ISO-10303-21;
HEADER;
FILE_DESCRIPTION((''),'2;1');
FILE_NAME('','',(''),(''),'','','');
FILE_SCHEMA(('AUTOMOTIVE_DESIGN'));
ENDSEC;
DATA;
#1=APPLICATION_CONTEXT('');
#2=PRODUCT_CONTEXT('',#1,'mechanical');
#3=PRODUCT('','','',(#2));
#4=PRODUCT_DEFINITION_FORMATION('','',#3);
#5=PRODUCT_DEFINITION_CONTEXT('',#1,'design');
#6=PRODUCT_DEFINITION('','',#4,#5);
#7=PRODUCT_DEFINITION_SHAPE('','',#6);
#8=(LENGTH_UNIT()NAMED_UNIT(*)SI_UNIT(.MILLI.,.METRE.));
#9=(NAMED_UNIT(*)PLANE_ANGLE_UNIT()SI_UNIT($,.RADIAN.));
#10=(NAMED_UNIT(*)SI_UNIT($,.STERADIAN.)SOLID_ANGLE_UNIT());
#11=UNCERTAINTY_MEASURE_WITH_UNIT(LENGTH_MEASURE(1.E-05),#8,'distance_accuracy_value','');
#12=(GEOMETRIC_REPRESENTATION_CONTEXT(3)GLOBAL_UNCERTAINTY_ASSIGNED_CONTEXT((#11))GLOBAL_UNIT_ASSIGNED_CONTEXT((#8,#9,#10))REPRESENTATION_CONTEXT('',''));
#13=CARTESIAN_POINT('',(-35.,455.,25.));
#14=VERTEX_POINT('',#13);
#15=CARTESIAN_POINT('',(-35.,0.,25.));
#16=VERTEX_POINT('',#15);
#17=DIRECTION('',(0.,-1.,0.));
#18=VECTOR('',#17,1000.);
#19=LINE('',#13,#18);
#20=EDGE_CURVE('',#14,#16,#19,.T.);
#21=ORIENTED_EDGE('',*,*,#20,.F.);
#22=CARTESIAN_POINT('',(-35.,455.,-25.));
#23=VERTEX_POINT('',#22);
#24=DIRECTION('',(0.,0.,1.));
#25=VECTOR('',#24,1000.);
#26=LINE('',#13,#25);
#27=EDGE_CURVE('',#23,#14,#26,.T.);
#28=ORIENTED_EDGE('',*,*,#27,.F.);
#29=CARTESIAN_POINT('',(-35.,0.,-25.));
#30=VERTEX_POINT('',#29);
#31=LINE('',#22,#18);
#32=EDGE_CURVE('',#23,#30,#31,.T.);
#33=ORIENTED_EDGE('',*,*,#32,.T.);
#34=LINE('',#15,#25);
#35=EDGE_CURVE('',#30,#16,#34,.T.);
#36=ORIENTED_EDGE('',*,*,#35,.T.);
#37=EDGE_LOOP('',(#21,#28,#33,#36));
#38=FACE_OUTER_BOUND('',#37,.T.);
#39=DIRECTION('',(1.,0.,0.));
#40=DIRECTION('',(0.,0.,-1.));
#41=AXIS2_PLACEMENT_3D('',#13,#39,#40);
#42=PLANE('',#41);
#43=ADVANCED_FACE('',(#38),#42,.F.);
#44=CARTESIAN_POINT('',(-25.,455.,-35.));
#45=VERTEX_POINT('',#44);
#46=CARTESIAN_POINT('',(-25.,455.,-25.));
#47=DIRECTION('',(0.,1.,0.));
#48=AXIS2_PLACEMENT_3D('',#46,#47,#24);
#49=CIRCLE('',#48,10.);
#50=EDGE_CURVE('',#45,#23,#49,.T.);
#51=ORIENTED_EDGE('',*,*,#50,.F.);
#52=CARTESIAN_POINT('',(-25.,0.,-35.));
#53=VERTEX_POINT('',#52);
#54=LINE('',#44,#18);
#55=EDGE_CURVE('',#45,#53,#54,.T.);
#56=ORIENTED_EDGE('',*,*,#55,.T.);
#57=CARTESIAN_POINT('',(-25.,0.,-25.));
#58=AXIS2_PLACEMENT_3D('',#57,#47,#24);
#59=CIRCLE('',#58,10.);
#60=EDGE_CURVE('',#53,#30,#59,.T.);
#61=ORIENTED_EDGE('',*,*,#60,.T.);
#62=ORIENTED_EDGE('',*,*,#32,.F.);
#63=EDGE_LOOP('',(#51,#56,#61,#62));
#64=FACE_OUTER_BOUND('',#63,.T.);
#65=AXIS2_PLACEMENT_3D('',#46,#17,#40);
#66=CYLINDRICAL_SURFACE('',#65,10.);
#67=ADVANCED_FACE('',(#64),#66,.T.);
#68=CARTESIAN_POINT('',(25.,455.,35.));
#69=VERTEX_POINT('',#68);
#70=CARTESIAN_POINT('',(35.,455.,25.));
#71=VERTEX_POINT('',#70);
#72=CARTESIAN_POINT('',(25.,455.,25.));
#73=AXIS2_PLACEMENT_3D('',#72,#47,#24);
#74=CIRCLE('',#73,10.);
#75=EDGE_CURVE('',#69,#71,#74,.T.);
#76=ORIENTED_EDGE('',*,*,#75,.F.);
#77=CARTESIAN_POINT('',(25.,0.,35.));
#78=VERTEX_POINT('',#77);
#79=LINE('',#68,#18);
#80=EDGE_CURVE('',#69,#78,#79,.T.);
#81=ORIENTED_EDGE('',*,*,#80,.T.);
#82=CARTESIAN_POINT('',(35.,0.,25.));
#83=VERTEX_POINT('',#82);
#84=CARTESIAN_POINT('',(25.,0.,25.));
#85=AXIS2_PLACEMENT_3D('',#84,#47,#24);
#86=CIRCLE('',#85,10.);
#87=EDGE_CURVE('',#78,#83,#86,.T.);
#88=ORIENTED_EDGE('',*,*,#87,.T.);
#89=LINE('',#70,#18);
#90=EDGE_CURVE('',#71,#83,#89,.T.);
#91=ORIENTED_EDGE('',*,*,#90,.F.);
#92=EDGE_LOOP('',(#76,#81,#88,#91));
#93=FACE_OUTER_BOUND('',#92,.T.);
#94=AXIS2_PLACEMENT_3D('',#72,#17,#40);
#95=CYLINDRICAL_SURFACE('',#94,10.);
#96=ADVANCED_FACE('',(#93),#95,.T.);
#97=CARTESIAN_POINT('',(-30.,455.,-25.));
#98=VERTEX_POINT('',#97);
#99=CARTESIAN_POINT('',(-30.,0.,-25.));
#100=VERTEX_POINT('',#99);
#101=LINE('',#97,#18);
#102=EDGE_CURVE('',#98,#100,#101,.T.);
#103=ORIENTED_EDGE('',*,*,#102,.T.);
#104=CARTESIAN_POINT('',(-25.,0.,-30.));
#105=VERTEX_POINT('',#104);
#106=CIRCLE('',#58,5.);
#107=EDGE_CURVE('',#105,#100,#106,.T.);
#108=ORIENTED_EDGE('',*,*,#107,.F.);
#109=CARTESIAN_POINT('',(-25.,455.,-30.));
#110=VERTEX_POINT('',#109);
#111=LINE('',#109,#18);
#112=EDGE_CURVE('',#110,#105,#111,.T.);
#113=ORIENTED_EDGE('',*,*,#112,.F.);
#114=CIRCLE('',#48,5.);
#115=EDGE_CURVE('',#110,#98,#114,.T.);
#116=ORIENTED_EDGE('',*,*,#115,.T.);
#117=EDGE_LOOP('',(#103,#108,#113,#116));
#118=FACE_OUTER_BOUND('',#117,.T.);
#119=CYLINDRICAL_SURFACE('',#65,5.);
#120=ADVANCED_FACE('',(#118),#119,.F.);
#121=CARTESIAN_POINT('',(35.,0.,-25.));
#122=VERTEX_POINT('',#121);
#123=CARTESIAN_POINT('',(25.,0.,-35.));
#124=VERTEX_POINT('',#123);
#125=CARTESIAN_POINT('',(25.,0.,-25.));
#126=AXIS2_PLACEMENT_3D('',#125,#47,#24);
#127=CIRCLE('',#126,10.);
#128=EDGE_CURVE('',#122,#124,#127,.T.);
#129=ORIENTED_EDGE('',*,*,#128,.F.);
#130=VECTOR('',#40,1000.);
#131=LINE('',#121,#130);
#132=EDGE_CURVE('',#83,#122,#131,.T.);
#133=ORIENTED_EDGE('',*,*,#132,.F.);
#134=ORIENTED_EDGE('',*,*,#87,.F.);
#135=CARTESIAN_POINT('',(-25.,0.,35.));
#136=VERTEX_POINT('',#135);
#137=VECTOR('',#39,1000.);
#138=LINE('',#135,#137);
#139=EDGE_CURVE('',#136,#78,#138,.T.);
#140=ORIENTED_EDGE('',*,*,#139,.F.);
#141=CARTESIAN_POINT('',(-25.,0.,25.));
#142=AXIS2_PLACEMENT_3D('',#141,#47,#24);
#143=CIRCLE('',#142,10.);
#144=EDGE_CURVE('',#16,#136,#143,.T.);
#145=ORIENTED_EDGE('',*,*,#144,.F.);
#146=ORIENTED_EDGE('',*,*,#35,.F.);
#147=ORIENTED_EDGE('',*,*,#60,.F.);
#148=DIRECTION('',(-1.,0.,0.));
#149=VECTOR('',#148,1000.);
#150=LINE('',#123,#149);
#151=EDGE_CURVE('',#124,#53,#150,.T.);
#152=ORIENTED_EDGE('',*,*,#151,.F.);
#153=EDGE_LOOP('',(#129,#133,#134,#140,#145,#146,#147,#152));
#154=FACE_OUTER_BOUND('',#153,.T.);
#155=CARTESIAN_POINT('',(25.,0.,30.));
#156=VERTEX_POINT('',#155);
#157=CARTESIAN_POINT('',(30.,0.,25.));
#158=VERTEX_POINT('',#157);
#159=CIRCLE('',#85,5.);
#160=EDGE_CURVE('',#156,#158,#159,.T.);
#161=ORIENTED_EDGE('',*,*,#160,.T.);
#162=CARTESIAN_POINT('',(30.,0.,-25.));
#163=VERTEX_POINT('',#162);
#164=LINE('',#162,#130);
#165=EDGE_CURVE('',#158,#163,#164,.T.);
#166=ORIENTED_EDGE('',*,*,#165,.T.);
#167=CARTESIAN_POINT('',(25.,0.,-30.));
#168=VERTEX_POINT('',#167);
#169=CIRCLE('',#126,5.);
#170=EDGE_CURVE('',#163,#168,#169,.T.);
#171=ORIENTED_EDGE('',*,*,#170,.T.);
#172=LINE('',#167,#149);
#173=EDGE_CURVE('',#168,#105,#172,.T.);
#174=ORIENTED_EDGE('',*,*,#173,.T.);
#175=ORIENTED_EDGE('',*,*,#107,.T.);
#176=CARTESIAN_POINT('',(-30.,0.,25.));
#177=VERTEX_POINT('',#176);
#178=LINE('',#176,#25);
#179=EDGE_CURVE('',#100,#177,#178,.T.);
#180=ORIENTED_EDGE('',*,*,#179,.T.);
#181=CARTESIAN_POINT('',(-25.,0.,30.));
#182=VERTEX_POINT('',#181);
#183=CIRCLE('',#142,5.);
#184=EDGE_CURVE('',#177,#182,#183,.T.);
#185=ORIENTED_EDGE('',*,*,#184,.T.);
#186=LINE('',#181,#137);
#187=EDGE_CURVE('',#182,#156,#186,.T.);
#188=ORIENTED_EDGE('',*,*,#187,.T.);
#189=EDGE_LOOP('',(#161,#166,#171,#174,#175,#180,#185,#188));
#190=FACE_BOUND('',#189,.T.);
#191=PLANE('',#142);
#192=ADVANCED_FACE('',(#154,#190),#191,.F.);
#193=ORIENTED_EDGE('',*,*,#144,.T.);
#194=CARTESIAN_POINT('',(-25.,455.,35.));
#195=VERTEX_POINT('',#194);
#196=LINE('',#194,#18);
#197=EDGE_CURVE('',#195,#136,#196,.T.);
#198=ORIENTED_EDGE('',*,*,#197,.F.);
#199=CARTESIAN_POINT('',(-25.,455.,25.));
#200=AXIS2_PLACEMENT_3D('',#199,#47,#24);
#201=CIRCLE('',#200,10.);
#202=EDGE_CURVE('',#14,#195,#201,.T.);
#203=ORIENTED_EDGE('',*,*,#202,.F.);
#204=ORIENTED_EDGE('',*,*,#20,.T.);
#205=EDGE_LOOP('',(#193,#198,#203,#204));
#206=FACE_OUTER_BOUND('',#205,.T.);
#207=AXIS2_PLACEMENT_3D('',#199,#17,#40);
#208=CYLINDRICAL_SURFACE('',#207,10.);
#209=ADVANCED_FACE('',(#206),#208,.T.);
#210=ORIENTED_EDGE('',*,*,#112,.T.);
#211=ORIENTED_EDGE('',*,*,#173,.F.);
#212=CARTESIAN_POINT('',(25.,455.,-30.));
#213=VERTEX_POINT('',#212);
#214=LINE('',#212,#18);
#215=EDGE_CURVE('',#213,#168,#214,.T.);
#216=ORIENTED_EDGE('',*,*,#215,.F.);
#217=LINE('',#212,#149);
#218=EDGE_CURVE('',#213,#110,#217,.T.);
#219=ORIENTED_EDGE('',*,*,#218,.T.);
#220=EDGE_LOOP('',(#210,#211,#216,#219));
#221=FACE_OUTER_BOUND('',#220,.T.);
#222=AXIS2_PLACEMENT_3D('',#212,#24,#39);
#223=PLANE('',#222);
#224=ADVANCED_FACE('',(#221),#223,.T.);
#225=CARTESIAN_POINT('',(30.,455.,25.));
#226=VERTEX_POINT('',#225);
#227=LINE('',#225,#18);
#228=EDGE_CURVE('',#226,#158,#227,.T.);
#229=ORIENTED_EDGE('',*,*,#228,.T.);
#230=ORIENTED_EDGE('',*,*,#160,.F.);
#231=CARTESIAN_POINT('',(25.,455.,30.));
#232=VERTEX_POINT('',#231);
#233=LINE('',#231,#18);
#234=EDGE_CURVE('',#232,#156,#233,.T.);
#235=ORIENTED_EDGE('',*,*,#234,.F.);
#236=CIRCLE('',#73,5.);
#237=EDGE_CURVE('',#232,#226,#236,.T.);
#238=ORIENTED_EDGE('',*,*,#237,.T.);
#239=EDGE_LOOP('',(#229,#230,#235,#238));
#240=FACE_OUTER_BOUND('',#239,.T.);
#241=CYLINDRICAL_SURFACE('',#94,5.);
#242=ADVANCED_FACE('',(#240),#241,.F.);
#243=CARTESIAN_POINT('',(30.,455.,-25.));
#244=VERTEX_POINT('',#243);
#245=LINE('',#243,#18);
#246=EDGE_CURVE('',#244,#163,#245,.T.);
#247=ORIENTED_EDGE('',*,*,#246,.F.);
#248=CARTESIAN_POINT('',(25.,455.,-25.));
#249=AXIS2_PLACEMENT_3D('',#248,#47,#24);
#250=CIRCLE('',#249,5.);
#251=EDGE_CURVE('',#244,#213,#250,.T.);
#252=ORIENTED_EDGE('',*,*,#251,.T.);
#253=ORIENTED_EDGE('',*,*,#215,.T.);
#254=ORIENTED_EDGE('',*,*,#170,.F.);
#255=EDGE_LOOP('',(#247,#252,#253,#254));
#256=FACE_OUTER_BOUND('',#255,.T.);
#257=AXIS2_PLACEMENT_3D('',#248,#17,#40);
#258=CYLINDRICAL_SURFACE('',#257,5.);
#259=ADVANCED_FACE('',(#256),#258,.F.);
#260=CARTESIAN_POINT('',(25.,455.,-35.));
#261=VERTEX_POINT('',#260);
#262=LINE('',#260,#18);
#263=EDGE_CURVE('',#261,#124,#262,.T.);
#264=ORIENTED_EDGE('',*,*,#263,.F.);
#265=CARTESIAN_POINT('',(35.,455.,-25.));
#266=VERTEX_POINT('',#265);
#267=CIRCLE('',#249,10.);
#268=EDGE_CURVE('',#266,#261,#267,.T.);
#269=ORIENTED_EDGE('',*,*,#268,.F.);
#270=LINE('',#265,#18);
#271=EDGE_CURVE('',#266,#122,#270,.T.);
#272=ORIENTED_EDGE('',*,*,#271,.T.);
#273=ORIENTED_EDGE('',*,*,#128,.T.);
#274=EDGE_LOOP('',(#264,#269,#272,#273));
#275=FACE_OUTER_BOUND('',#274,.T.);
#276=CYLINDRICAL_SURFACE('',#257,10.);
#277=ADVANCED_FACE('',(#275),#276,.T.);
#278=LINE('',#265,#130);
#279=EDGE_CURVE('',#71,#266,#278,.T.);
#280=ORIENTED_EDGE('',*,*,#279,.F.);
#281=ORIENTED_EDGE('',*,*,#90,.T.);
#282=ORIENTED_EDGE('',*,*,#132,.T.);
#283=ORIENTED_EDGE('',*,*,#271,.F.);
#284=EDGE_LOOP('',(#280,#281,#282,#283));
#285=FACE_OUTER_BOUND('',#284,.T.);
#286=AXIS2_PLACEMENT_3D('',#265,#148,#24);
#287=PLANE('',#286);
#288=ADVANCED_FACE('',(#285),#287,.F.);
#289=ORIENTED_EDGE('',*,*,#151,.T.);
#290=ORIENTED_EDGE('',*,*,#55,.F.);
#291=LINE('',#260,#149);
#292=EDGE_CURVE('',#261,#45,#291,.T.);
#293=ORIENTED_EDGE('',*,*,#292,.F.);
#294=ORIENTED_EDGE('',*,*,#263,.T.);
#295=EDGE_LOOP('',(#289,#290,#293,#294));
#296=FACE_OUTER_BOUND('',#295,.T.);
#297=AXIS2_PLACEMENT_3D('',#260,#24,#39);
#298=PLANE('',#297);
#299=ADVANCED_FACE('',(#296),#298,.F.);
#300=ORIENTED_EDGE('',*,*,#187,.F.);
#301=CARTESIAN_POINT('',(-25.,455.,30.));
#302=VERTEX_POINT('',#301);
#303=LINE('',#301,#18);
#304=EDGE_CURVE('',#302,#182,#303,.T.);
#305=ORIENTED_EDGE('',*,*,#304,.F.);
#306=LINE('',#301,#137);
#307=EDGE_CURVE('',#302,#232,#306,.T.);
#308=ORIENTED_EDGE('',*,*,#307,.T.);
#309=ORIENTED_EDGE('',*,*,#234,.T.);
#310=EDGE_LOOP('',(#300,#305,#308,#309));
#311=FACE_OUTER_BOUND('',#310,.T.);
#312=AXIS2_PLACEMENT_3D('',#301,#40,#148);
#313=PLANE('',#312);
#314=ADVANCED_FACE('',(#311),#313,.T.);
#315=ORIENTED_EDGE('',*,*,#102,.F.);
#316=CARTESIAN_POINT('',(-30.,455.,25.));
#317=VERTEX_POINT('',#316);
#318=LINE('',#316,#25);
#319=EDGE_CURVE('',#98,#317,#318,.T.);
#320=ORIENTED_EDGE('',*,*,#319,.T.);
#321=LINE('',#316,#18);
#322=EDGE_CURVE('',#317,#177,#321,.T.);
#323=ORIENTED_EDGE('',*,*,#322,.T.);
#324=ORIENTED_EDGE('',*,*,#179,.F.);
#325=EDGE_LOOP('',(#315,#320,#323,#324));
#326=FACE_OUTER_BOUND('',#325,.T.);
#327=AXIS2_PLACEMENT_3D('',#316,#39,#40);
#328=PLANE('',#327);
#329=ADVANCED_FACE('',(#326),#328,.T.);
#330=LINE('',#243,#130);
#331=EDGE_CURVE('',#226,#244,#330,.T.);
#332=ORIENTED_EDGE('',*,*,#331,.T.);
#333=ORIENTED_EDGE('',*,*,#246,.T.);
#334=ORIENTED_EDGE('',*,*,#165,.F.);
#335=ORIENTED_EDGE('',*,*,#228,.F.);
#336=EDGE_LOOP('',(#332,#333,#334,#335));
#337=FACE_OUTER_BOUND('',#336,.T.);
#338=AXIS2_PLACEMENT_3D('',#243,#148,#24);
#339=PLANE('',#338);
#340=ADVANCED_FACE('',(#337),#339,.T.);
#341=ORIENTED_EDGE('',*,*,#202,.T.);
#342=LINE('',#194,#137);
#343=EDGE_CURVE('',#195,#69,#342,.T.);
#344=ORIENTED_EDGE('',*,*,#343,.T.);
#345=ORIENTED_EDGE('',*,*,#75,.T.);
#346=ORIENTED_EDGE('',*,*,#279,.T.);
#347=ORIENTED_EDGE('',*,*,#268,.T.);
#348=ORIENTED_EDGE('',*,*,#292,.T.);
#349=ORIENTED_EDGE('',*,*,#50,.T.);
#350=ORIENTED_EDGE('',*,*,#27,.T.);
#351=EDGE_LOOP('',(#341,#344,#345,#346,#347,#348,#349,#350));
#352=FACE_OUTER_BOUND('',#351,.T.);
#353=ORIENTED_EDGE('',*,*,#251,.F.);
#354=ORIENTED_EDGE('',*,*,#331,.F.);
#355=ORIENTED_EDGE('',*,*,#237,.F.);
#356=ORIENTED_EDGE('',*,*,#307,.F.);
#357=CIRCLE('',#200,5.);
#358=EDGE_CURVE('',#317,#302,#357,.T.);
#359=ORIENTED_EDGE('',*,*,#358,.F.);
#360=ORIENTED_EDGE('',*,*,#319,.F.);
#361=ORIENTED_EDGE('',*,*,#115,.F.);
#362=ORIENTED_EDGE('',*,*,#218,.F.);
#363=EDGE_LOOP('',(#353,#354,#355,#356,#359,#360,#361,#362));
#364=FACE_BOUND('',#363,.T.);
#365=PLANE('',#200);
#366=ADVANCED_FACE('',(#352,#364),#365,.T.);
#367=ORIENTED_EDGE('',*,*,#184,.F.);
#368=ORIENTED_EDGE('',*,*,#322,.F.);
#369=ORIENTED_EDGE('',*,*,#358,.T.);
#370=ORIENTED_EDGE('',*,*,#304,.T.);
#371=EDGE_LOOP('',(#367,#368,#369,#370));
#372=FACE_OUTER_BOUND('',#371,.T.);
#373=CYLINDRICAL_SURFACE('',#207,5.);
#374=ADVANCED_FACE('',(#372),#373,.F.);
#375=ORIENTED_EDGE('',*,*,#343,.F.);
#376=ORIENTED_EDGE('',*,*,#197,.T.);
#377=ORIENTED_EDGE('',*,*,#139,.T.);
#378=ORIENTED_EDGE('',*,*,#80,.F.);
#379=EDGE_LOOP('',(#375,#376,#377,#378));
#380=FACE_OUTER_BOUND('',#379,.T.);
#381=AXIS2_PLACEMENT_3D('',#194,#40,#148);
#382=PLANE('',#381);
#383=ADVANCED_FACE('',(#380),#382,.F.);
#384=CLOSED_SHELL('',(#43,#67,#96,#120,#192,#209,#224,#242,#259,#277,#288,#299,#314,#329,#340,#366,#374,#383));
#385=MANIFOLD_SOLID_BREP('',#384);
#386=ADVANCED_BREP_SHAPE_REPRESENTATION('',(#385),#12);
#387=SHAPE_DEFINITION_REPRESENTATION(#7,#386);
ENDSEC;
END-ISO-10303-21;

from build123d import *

# Parameters (mm, degrees)
GB_T6728_2002_70_70_5_1_DEPTH = 455


with BuildPart() as part:
    # Sketch1 → 结构用冷弯空心方钢(gb t6728-2002) 70×70×5(1) (new body)
    with BuildSketch(Plane(origin=(0, 0, 0), x_dir=(-1, 0, 0), z_dir=(0, 1, 0))):
        with BuildLine():
            Line((-25, -35), (25, -35))
            ThreePointArc((25, -35), (32.071067812, -32.071067812), (35, -25))
            Line((35, -25), (35, 25))
            ThreePointArc((35, 25), (32.071067812, 32.071067812), (25, 35))
            Line((25, 35), (-25, 35))
            ThreePointArc((-25, 35), (-32.071067812, 32.071067812), (-35, 25))
            Line((-35, 25), (-35, -25))
            ThreePointArc((-35, -25), (-32.071067812, -32.071067812), (-25, -35))
        make_face()
        with BuildLine():
            Line((-25, -30), (25, -30))
            ThreePointArc((25, -30), (28.535533906, -28.535533906), (30, -25))
            Line((30, -25), (30, 25))
            ThreePointArc((30, 25), (28.535533906, 28.535533906), (25, 30))
            Line((25, 30), (-25, 30))
            ThreePointArc((-25, 30), (-28.535533906, 28.535533906), (-30, 25))
            Line((-30, 25), (-30, -25))
            ThreePointArc((-30, -25), (-28.535533906, -28.535533906), (-25, -30))
        make_face(mode=Mode.SUBTRACT)
    extrude(amount=GB_T6728_2002_70_70_5_1_DEPTH)


solid = part.part
